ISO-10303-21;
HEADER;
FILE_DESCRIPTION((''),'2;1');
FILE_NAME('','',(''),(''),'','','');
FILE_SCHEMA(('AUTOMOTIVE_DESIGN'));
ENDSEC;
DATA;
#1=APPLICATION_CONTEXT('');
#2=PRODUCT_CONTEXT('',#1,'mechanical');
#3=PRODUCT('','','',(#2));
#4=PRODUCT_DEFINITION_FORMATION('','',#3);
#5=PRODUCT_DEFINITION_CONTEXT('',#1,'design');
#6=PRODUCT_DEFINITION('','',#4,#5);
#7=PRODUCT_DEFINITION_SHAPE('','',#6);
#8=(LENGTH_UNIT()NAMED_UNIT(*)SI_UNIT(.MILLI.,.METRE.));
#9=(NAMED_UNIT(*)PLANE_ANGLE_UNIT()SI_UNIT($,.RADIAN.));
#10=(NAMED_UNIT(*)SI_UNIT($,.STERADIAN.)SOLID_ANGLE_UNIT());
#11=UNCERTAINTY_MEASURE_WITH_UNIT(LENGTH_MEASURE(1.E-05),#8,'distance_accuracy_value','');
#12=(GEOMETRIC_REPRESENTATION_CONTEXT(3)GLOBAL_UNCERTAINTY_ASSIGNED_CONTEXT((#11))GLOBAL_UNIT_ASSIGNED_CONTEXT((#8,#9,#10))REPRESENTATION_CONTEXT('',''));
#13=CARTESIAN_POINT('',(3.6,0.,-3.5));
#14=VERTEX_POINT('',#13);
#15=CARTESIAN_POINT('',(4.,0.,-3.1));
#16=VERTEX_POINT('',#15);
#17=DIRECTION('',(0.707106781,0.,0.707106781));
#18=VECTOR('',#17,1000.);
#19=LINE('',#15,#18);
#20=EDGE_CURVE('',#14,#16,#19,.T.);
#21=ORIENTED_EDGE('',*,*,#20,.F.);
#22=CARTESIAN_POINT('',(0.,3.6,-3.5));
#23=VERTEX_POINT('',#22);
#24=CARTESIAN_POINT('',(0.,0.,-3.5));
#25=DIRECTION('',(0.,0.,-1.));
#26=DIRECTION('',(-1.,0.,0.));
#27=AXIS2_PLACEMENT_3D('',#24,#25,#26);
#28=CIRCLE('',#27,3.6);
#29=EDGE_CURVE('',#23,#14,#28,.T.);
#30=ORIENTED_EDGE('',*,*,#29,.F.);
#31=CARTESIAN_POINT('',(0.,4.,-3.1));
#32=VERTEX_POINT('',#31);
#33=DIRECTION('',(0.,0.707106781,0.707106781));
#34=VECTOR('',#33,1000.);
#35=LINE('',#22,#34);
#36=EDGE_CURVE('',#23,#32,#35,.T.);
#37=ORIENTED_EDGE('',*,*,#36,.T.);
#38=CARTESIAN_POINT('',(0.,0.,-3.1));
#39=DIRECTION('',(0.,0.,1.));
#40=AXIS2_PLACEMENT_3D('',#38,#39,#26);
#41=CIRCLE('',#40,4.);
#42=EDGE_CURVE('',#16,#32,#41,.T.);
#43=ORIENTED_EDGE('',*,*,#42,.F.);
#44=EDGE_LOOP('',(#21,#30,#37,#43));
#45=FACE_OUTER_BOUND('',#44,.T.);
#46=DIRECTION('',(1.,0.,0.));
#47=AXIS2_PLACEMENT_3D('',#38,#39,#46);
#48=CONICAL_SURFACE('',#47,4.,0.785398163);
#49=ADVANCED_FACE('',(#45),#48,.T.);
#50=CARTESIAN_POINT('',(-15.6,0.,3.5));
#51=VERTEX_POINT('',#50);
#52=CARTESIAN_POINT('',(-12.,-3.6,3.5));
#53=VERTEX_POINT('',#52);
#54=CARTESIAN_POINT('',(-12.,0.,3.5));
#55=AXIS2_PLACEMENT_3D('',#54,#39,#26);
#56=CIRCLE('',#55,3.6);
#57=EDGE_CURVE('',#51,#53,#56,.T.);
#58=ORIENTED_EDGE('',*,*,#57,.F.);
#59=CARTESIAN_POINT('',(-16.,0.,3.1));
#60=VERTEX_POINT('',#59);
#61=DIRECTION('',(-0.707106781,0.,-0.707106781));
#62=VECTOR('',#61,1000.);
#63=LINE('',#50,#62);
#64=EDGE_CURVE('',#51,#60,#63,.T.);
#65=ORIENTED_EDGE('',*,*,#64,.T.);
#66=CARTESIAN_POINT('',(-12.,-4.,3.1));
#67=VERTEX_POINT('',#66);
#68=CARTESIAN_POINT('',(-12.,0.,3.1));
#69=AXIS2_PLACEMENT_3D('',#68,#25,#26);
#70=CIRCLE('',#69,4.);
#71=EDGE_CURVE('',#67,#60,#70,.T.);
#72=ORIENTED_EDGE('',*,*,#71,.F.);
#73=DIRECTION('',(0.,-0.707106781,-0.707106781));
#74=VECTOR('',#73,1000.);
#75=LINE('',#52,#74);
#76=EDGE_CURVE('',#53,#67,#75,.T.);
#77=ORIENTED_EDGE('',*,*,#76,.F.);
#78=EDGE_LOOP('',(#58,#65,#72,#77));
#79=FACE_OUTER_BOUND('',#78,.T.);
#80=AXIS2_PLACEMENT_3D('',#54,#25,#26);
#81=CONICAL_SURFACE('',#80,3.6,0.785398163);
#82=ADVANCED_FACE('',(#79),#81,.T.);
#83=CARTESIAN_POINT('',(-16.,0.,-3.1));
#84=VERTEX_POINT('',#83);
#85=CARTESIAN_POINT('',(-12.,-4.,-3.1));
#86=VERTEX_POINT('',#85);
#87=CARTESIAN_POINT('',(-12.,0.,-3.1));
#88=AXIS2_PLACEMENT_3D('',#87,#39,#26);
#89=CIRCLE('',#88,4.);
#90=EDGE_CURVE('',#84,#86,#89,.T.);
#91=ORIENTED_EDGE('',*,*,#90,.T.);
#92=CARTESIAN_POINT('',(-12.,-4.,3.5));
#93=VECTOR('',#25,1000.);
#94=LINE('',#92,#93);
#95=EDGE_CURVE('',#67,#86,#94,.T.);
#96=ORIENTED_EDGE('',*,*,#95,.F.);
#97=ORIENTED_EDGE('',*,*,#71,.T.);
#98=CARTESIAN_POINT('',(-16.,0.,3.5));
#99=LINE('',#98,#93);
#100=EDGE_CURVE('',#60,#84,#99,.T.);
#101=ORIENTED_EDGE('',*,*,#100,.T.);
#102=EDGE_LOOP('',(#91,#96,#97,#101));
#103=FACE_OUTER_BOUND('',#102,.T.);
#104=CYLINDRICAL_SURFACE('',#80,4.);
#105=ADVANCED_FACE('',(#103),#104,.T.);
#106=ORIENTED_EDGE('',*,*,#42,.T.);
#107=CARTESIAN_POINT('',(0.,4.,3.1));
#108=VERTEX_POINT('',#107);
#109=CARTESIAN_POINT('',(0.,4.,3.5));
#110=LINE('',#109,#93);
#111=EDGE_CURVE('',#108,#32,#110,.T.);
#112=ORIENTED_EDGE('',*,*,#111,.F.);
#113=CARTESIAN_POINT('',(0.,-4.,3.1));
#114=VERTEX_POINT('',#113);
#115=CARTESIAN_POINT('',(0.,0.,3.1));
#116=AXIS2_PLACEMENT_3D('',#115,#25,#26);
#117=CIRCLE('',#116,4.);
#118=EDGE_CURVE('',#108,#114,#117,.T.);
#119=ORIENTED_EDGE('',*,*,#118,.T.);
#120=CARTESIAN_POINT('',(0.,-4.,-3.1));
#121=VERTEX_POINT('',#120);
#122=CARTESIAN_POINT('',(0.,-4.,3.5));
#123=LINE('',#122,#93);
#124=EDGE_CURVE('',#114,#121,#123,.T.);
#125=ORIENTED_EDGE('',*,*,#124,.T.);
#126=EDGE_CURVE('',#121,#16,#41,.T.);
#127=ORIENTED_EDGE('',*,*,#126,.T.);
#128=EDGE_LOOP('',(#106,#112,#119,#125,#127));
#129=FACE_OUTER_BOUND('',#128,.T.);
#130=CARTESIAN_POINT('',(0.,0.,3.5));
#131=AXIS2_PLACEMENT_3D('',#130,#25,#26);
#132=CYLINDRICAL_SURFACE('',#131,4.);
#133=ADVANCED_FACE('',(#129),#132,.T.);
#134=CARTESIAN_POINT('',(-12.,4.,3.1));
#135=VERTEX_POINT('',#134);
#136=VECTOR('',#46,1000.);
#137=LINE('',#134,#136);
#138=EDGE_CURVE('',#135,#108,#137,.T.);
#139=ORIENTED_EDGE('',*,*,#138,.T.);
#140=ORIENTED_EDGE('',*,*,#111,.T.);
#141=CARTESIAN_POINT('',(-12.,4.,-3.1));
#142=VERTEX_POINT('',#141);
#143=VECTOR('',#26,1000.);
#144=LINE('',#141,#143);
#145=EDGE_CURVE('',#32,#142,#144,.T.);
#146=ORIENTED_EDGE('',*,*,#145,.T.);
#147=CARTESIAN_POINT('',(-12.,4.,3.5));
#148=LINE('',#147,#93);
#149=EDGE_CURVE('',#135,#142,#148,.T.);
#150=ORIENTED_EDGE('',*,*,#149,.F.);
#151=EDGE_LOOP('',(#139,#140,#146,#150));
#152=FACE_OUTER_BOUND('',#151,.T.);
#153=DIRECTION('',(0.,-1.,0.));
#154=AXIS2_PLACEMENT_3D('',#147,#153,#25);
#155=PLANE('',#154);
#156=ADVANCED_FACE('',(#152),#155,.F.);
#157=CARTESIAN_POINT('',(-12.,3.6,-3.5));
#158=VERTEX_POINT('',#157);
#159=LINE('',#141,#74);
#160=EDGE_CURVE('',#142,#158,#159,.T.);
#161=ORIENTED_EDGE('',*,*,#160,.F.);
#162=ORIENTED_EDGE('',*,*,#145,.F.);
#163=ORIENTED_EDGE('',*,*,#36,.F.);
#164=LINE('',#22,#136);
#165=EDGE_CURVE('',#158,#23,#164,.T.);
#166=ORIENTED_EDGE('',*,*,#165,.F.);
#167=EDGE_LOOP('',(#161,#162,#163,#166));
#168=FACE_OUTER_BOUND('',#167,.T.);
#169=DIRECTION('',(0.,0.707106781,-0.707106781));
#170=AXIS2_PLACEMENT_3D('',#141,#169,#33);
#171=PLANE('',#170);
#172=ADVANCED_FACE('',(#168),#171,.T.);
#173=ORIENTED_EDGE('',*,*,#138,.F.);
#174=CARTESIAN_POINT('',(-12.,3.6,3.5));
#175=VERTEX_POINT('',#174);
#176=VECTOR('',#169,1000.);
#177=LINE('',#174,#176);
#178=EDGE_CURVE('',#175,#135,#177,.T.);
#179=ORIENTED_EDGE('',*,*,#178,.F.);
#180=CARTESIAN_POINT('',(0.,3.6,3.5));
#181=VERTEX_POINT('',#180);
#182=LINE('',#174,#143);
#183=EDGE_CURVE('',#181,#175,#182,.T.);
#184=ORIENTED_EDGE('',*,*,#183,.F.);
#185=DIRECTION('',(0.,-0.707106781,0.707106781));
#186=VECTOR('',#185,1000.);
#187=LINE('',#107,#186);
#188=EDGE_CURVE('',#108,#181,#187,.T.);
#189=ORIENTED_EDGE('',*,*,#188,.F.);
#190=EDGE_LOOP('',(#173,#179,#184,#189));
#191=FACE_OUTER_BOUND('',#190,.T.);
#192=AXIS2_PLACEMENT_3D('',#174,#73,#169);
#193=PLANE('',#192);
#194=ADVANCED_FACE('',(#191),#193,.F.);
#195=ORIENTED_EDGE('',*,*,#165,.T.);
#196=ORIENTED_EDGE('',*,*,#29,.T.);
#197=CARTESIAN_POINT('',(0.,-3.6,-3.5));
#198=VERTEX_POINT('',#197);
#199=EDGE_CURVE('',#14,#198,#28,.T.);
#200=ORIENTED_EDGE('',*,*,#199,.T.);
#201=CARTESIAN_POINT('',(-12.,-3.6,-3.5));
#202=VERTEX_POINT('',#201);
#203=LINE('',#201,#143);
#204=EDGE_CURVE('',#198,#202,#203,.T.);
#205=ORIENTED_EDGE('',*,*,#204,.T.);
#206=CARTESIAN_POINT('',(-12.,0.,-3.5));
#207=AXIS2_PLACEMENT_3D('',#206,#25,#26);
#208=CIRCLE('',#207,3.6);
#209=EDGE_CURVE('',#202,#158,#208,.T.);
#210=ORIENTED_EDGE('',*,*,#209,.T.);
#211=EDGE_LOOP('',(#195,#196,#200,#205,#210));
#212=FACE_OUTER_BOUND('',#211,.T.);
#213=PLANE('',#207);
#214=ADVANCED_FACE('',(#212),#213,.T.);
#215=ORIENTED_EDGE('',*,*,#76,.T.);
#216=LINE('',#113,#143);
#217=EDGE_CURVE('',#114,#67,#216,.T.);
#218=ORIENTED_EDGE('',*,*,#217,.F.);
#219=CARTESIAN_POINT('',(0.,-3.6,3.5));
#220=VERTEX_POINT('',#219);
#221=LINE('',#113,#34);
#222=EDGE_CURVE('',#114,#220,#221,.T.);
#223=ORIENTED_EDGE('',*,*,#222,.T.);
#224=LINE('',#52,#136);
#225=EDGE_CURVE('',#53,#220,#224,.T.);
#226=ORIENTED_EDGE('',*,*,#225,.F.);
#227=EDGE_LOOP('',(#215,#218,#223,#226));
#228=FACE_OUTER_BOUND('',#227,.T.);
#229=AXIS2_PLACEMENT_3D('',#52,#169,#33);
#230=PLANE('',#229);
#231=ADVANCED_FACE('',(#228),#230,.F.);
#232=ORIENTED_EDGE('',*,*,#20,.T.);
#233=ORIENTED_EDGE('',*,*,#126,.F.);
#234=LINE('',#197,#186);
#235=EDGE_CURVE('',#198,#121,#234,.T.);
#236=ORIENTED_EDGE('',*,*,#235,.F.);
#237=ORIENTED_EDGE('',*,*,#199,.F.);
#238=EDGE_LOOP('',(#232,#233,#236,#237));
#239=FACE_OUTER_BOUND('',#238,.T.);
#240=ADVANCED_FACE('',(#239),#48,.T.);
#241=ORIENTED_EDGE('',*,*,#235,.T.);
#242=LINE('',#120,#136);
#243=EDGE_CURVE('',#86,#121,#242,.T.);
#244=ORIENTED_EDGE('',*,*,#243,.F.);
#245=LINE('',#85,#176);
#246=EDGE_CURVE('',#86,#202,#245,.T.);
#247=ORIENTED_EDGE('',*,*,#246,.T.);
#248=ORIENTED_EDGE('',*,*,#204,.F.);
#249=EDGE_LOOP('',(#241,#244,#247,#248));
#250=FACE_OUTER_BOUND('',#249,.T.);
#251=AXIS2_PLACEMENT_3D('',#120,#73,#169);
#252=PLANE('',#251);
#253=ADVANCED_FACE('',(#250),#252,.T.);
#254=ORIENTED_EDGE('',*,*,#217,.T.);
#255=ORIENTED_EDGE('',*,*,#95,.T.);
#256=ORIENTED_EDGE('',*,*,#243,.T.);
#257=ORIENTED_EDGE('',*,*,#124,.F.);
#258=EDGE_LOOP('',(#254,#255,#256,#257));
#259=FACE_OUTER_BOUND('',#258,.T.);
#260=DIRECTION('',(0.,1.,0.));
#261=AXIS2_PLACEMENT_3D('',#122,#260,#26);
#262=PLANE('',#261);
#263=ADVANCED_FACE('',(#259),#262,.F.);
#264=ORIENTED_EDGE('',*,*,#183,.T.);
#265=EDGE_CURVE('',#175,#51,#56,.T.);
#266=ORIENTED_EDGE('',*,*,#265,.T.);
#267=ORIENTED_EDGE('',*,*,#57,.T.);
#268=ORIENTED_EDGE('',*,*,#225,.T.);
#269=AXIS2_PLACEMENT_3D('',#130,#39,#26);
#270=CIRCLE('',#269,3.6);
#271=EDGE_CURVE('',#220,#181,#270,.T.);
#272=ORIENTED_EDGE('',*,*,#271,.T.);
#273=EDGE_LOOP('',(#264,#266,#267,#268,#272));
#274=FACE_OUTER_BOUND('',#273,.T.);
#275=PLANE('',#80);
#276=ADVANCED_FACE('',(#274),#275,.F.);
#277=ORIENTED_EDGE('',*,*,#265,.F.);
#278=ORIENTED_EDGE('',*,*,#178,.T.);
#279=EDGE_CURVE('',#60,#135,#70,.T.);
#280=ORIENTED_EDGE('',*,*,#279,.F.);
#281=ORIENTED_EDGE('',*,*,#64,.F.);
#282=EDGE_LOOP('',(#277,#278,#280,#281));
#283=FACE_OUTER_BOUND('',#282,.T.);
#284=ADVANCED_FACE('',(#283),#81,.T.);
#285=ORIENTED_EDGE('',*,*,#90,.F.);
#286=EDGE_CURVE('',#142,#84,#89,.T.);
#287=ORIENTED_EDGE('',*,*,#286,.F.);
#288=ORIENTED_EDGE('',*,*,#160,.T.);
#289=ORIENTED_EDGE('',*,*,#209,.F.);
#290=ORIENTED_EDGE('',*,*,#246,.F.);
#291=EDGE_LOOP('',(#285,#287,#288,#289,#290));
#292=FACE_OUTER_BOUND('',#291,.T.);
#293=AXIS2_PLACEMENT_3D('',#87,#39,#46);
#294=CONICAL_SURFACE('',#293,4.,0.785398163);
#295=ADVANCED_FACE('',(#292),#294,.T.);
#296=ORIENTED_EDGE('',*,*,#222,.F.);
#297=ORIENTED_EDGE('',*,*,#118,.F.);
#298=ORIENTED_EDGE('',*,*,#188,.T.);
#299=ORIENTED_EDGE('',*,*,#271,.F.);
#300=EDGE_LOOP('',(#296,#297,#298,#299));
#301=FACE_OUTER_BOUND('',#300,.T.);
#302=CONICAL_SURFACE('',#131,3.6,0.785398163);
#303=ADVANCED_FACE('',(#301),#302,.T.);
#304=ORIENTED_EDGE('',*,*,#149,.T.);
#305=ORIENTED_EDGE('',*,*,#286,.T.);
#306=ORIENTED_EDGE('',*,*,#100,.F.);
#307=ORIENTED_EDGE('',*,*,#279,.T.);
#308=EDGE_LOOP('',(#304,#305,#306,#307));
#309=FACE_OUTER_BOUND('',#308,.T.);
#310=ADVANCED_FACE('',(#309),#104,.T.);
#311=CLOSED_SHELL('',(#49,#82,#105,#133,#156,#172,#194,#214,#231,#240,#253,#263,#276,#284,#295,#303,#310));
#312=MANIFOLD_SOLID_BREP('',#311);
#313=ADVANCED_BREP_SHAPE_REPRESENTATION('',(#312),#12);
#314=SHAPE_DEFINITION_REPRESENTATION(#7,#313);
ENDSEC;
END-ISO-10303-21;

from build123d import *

# Parameters (mm, degrees)
BASEKEY_DEPTH = 3.5
CHAMFER1_SIZE = 0.4


with BuildPart() as part:
    # Sketch1 → BaseKey (new, symmetric)
    with BuildSketch(Plane.XY):
        with BuildLine():
            Line((-12, 4), (0, 4))
            ThreePointArc((0, 4), (4, 0), (0, -4))
            Line((0, -4), (-12, -4))
            ThreePointArc((-12, -4), (-16, 0), (-12, 4))
        make_face()
    extrude(amount=BASEKEY_DEPTH, both=True)

    # Chamfer1
    chamfer1_edges = [part.edges().sort_by_distance(p)[0] for p in [
        (4, 0, 3.5),
        (-6, 4, 3.5),
        (-16, 0, 3.5),
        (-6, 4, -3.5),
        (4, 0, -3.5),
        (-6, -4, -3.5),
        (-16, 0, -3.5),
        (-6, -4, 3.5),
    ]]
    chamfer(chamfer1_edges, length=CHAMFER1_SIZE)


solid = part.part
